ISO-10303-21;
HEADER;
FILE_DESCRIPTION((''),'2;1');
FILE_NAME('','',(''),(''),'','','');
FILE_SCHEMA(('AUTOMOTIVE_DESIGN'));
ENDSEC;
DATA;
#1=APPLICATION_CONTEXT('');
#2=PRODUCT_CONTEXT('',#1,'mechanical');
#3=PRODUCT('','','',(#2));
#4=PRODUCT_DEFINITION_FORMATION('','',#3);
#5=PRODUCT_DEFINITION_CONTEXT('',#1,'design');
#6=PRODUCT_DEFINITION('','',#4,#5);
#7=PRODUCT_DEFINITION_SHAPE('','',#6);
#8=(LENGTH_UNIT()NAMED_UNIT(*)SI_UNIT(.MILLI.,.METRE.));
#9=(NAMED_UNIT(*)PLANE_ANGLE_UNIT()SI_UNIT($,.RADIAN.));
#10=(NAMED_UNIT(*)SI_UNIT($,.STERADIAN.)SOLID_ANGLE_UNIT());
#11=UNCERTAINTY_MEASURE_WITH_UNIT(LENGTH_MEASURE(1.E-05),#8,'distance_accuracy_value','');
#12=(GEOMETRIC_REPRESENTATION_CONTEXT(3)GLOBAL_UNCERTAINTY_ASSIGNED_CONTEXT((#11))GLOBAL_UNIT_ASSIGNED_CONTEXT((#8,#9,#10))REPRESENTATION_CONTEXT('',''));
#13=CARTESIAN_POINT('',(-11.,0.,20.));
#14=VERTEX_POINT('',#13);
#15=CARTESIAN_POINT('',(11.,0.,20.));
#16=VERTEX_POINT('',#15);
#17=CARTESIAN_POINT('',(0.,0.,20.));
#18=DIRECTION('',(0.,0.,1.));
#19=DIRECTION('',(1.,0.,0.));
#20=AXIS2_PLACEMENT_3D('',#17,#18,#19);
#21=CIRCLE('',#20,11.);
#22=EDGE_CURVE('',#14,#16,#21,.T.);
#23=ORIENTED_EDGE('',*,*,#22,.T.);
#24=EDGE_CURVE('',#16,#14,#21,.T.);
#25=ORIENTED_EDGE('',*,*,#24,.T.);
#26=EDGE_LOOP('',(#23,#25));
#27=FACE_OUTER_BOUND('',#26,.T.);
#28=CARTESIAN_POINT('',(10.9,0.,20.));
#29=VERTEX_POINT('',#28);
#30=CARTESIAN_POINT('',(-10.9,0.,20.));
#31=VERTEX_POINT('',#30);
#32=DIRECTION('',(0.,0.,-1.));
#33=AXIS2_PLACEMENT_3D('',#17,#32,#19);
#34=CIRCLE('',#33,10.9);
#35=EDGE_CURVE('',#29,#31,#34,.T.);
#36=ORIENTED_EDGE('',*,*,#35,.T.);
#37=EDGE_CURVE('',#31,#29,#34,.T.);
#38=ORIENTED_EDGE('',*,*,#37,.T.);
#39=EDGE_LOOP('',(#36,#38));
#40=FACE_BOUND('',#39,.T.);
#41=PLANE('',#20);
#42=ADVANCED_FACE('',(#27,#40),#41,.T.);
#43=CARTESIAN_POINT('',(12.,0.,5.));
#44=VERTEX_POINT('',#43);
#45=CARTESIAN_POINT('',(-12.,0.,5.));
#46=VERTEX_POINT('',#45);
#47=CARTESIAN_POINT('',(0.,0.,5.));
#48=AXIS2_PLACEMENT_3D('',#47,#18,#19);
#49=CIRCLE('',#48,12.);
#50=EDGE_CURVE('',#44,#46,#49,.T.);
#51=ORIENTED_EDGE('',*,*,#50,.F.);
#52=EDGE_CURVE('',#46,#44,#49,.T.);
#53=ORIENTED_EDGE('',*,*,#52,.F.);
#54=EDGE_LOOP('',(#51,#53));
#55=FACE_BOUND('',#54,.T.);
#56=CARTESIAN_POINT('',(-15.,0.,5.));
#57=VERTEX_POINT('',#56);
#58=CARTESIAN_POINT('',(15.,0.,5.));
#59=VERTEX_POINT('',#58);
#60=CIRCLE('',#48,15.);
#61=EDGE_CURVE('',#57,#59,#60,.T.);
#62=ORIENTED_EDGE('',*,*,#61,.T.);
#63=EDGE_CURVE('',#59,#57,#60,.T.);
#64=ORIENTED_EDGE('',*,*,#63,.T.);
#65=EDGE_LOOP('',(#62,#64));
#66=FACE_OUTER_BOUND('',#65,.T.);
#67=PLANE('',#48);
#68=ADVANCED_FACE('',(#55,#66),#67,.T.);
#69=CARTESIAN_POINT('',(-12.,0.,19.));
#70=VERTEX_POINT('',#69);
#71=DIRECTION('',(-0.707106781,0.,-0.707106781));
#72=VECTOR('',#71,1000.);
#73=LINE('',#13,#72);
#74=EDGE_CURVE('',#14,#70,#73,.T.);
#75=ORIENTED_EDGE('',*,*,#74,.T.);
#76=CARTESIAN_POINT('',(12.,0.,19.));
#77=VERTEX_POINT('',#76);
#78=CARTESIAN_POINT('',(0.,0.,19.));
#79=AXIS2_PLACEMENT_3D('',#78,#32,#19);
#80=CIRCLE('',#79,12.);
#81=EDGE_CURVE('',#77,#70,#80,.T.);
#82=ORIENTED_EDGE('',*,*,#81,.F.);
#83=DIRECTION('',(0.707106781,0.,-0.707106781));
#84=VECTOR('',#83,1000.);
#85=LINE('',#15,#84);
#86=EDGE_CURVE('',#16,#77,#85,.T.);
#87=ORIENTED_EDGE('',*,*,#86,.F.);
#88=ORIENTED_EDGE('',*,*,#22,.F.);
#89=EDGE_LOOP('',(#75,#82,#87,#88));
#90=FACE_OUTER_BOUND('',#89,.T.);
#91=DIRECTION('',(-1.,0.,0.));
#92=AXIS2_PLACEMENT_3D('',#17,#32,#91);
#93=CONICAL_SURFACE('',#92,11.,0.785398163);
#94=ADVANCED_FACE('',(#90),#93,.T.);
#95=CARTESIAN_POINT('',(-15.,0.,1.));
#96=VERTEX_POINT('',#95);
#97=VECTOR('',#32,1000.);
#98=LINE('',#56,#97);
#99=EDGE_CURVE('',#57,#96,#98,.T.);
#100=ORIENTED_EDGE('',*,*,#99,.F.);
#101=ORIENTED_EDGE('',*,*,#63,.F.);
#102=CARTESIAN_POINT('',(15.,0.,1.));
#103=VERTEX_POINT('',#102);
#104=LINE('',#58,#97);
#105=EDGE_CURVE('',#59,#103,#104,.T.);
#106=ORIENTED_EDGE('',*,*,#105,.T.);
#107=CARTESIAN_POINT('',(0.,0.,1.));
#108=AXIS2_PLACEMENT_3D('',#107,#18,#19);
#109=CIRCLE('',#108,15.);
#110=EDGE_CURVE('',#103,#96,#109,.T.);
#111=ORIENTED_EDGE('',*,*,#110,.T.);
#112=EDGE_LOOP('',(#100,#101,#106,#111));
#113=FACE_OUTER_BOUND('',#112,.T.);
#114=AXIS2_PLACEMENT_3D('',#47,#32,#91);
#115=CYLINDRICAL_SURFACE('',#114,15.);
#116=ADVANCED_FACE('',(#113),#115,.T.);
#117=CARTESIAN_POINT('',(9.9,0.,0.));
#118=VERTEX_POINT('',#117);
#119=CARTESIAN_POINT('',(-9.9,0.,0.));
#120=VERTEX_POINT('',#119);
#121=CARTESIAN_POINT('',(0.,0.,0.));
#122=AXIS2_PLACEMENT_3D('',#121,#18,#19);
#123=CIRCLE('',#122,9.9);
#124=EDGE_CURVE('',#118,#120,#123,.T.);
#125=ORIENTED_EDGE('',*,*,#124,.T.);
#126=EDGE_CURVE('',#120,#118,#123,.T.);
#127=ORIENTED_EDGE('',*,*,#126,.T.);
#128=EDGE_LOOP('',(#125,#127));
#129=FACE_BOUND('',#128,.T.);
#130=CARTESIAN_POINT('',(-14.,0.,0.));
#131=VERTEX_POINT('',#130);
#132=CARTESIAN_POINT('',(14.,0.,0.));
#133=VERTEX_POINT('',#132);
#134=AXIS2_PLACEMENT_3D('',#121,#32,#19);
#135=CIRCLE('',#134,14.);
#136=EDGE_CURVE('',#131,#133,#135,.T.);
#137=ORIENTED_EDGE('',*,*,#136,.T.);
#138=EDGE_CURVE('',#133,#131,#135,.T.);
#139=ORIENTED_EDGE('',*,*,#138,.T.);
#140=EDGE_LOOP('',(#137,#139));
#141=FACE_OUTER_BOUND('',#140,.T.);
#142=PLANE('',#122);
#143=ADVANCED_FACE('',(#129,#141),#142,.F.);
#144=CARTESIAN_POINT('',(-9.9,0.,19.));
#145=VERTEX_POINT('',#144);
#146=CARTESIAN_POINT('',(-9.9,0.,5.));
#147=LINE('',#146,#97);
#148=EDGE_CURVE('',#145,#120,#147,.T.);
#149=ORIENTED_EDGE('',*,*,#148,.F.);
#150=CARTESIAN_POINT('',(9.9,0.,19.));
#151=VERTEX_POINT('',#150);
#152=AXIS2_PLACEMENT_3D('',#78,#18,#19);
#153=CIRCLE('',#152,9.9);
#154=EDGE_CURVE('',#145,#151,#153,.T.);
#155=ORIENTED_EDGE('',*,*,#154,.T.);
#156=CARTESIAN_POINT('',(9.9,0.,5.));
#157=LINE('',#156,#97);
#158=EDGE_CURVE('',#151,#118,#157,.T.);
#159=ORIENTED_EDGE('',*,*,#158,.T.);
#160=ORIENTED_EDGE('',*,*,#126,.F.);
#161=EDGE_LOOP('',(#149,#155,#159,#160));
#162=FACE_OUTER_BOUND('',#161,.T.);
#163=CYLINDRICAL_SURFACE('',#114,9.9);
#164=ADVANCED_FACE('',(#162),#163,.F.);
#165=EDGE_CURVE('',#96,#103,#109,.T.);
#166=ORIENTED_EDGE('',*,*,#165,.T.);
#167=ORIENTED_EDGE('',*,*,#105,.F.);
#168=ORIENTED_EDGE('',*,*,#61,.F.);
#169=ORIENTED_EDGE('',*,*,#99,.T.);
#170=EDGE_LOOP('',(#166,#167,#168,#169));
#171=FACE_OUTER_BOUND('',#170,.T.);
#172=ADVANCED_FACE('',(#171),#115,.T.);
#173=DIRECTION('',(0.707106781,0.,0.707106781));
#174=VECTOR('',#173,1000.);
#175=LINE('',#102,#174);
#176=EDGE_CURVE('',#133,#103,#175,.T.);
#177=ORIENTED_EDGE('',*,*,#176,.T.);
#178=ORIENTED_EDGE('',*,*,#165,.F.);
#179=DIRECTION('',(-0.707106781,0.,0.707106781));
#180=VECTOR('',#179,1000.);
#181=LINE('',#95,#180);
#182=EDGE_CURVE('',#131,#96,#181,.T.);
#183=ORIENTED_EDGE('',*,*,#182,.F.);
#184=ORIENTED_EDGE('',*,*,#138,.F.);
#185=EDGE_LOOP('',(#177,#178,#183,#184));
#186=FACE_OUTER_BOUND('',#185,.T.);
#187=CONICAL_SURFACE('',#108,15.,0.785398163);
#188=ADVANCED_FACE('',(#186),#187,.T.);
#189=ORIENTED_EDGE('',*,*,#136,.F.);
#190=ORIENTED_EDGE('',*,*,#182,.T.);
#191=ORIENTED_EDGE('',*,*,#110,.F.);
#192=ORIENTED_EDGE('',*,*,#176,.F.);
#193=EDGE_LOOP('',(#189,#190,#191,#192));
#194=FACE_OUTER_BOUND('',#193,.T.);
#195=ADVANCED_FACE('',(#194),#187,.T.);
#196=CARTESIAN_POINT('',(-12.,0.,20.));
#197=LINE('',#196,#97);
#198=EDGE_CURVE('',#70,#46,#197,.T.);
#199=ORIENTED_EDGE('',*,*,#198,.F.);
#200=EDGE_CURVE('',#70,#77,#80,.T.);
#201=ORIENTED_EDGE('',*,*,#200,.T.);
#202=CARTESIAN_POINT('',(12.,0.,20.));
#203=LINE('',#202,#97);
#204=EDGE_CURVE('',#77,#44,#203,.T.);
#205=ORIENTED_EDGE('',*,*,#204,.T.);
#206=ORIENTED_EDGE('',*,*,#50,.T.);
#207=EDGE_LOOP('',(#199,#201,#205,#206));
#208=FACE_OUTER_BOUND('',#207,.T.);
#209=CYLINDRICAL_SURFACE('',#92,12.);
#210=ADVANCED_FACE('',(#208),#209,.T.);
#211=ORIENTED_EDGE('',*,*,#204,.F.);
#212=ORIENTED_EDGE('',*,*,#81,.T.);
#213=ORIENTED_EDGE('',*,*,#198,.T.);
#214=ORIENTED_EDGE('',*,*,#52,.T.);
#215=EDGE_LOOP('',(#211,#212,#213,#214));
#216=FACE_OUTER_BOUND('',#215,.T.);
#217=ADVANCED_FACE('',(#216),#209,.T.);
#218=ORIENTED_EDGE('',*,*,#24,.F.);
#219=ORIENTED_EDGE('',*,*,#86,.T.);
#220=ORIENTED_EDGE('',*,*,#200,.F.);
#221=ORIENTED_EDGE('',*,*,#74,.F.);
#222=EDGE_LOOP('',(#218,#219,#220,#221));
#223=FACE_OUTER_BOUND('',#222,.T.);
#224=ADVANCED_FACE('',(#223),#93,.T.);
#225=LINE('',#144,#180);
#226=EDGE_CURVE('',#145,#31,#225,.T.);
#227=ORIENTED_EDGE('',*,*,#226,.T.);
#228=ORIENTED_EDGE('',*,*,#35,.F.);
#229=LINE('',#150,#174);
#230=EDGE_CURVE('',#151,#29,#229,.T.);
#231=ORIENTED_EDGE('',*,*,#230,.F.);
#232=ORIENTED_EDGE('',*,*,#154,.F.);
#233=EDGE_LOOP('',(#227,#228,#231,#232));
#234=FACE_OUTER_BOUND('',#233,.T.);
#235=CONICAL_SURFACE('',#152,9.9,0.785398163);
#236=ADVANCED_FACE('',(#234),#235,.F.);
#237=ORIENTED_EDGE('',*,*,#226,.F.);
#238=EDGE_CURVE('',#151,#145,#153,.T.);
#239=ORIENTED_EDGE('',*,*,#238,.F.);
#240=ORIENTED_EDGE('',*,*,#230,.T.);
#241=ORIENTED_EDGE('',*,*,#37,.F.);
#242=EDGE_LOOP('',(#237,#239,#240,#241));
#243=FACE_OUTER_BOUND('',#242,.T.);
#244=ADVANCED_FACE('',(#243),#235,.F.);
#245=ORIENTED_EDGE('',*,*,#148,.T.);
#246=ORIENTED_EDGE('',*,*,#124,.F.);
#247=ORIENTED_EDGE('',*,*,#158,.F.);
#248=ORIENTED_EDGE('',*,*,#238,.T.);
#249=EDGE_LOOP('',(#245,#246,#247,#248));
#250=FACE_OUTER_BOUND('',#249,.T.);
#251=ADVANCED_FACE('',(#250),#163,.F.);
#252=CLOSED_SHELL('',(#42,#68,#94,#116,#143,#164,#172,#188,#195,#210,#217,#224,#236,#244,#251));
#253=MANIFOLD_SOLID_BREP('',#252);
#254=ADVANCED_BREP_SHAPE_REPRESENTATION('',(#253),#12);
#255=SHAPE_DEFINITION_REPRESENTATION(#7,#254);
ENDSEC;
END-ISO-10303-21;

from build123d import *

# Parameters (mm, degrees)
SKETCH1_R           = 15
SKETCH1_R_2         = 9.9
BOSS_EXTRUDE1_DEPTH = 5
SKETCH2_R           = 12
SKETCH2_R_2         = 9.9
BOSS_EXTRUDE2_DEPTH = 15
CHAMFER1_SIZE       = 1


with BuildPart() as part:
    # Sketch1 → Boss-Extrude1 (new body)
    with BuildSketch(Plane.XY):
        Circle(SKETCH1_R)
        Circle(SKETCH1_R_2, mode=Mode.SUBTRACT)
    extrude(amount=BOSS_EXTRUDE1_DEPTH)

    # Sketch2 → Boss-Extrude2 (add)
    with BuildSketch(Plane.XY.offset(5)):
        Circle(SKETCH2_R)
        Circle(SKETCH2_R_2, mode=Mode.SUBTRACT)
    extrude(amount=BOSS_EXTRUDE2_DEPTH)

    # Chamfer1
    chamfer1_edges = [part.edges().sort_by_distance(p)[0] for p in [
        (-12, 0, 20),
        (-9.9, 0, 20),
        (-15, 0, 0),
    ]]
    chamfer(chamfer1_edges, length=CHAMFER1_SIZE)


solid = part.part
